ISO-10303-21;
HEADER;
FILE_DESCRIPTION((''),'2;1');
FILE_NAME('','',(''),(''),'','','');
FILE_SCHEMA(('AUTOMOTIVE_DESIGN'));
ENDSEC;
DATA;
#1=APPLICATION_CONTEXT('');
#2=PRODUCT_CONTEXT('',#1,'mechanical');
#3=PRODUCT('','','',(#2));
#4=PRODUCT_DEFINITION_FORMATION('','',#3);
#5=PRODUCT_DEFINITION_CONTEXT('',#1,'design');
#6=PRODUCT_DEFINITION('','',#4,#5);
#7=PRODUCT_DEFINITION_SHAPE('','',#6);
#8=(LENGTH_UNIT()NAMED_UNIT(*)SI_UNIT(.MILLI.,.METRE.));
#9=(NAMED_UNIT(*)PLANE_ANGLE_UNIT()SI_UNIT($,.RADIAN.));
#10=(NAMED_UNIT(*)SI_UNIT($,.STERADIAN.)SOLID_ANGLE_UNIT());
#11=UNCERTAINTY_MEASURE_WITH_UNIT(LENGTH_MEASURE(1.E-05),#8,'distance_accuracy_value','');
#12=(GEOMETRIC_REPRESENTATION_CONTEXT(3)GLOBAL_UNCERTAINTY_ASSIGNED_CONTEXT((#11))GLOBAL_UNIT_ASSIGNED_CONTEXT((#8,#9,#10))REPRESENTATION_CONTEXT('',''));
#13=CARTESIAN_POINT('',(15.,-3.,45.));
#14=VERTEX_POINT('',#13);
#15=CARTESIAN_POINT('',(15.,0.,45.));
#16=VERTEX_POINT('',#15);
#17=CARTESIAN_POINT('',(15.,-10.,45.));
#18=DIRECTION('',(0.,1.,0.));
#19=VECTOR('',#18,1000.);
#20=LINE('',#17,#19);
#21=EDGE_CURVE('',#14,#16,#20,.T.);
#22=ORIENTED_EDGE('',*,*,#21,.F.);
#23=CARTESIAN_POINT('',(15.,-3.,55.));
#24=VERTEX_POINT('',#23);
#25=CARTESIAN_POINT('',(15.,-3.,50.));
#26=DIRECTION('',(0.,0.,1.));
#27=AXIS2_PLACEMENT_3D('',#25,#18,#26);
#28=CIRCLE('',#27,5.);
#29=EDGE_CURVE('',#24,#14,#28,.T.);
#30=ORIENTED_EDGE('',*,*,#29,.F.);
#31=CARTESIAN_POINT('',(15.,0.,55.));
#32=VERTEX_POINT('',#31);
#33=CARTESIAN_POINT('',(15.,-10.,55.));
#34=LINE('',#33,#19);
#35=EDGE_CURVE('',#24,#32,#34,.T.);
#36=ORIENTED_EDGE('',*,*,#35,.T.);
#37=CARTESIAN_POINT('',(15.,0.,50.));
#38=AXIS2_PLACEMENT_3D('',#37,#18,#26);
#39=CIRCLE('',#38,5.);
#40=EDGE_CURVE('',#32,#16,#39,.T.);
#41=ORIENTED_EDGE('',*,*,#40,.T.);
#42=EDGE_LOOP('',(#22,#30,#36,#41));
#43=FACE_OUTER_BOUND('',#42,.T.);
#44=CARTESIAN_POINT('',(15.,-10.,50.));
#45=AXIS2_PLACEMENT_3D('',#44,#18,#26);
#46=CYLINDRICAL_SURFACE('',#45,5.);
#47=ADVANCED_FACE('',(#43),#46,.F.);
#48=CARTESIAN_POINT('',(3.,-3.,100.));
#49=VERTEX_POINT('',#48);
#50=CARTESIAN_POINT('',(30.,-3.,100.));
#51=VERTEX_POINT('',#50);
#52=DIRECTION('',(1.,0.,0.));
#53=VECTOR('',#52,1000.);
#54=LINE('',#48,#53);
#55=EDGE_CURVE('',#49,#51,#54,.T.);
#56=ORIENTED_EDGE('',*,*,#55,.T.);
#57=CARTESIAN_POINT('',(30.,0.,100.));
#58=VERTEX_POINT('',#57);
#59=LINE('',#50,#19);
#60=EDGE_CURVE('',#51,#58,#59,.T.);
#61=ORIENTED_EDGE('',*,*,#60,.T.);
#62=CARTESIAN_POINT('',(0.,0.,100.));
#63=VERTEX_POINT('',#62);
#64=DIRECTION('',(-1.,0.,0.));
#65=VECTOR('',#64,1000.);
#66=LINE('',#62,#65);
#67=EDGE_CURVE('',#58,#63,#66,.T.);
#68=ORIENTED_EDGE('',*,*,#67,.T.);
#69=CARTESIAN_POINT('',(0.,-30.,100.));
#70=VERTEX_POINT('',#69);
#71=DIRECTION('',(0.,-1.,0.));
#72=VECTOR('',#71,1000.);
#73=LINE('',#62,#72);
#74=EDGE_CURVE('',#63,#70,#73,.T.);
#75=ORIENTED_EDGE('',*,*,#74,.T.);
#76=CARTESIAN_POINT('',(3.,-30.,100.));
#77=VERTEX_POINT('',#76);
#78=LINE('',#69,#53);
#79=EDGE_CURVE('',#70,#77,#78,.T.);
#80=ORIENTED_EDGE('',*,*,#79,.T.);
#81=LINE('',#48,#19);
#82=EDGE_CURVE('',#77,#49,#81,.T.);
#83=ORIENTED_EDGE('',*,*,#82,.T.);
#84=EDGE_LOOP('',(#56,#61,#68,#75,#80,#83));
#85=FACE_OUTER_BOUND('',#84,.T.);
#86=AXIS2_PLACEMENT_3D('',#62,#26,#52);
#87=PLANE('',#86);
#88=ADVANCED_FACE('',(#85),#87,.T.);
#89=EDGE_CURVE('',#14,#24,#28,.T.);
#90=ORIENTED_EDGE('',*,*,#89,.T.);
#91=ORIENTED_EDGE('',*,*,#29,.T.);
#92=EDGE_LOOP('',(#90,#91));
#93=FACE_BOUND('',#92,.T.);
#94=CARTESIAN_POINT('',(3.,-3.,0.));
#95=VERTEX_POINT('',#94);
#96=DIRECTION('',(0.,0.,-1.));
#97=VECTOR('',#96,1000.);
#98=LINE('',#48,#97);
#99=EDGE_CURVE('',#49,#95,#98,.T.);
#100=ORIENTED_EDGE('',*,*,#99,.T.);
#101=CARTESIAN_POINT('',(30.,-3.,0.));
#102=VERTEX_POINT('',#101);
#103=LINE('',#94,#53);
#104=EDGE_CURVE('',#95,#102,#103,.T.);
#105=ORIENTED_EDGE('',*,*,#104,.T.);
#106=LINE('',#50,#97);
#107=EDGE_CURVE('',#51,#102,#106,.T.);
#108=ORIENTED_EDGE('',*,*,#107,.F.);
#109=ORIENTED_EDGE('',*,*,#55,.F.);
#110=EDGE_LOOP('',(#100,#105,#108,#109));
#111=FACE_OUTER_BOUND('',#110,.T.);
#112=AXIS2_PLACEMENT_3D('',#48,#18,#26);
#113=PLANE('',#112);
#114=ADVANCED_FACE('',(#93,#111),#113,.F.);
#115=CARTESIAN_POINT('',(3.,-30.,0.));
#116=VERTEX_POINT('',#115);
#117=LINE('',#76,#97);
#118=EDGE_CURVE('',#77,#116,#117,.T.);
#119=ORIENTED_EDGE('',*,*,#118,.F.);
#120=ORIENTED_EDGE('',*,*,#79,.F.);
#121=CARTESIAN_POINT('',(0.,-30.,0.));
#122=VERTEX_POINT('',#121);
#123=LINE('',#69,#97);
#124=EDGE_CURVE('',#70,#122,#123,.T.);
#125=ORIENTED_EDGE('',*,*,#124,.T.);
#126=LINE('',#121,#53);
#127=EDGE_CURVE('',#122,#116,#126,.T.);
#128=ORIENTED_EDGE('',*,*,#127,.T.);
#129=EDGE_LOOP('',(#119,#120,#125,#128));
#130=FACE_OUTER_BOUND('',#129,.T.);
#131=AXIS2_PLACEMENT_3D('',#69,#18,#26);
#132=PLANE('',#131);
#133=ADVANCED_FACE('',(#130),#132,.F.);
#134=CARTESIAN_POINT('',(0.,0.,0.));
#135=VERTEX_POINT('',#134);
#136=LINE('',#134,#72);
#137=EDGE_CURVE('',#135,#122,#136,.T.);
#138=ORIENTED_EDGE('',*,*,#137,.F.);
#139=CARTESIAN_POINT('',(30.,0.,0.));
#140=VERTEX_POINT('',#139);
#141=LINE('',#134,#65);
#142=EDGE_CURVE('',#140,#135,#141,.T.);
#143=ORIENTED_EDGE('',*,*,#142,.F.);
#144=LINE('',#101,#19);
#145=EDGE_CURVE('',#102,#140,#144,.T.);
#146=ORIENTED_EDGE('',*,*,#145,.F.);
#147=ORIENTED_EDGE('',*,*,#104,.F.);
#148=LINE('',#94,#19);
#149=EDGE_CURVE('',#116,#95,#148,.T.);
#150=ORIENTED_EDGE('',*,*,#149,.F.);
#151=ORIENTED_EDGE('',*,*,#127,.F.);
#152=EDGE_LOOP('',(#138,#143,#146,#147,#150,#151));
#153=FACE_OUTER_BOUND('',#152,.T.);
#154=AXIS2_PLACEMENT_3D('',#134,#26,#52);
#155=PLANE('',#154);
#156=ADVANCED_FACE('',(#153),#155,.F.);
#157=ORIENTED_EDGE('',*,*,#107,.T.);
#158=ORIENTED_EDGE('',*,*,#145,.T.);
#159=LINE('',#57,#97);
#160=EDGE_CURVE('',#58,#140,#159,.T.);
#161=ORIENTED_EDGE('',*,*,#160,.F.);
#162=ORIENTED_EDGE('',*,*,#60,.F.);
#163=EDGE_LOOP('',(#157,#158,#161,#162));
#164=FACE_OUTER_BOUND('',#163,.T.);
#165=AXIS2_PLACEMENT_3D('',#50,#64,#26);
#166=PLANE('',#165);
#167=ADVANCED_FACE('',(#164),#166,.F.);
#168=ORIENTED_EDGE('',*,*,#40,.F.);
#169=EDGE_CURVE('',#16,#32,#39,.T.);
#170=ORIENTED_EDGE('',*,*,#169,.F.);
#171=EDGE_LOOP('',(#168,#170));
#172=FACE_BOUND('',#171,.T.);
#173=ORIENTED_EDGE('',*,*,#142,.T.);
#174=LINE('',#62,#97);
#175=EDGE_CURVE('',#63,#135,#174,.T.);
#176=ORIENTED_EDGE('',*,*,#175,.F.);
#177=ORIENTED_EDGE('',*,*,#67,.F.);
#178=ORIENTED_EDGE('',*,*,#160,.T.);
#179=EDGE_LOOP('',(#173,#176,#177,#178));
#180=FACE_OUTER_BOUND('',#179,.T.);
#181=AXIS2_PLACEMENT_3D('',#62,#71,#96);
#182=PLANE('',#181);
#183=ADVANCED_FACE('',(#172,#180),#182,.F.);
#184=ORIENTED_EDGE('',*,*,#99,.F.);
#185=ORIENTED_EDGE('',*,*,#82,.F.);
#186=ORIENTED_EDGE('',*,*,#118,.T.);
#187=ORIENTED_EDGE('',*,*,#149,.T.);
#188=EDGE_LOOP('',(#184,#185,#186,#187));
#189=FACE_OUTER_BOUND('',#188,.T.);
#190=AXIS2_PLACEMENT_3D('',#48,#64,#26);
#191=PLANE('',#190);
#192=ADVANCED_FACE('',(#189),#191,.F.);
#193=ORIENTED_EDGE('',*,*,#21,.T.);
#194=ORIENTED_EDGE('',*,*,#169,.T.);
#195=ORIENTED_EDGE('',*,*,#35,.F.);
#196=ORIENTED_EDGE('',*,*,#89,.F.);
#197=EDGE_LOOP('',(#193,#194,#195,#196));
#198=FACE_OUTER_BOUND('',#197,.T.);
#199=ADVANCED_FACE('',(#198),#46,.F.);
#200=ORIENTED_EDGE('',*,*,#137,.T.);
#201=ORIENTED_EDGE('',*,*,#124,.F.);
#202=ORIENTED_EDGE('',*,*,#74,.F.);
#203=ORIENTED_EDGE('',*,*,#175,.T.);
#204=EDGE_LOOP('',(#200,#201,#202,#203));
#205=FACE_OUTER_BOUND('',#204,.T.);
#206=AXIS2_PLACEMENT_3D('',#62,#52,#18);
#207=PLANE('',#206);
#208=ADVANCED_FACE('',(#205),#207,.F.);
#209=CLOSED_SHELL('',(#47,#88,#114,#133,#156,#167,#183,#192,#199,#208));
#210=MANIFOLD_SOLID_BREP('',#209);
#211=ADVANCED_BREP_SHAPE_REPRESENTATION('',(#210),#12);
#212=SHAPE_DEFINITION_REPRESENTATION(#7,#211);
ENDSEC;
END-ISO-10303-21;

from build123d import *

# Parameters (mm, degrees)
EXTRUDE_1_DEPTH     = 100
CUT_EXTRUDE_1_DEPTH = 10


with BuildPart() as part:
    # 草图1 → 凸台-拉伸1 (new body)
    with BuildSketch(Plane.XY):
        Polygon((0, 0), (30, 0), (30, -3), (3, -3), (3, -30), (0, -30), align=None)
    extrude(amount=EXTRUDE_1_DEPTH)

    # 草图2 → 切除-拉伸1 (cut)
    with BuildSketch(Plane(origin=(0, 0, 0), x_dir=(1, 0, 0), z_dir=(0, 1, 0))):
        with BuildLine():
            ThreePointArc((20, -50), (18.535533906, -46.464466094), (15, -45))
            Line((15, -45), (15, -55))
            ThreePointArc((15, -55), (18.535533906, -53.535533906), (20, -50))
        make_face()
        with BuildLine():
            Line((15, -55), (15, -45))
            ThreePointArc((15, -45), (10, -50), (15, -55))
        make_face()
    extrude(amount=-CUT_EXTRUDE_1_DEPTH, mode=Mode.SUBTRACT)


solid = part.part
